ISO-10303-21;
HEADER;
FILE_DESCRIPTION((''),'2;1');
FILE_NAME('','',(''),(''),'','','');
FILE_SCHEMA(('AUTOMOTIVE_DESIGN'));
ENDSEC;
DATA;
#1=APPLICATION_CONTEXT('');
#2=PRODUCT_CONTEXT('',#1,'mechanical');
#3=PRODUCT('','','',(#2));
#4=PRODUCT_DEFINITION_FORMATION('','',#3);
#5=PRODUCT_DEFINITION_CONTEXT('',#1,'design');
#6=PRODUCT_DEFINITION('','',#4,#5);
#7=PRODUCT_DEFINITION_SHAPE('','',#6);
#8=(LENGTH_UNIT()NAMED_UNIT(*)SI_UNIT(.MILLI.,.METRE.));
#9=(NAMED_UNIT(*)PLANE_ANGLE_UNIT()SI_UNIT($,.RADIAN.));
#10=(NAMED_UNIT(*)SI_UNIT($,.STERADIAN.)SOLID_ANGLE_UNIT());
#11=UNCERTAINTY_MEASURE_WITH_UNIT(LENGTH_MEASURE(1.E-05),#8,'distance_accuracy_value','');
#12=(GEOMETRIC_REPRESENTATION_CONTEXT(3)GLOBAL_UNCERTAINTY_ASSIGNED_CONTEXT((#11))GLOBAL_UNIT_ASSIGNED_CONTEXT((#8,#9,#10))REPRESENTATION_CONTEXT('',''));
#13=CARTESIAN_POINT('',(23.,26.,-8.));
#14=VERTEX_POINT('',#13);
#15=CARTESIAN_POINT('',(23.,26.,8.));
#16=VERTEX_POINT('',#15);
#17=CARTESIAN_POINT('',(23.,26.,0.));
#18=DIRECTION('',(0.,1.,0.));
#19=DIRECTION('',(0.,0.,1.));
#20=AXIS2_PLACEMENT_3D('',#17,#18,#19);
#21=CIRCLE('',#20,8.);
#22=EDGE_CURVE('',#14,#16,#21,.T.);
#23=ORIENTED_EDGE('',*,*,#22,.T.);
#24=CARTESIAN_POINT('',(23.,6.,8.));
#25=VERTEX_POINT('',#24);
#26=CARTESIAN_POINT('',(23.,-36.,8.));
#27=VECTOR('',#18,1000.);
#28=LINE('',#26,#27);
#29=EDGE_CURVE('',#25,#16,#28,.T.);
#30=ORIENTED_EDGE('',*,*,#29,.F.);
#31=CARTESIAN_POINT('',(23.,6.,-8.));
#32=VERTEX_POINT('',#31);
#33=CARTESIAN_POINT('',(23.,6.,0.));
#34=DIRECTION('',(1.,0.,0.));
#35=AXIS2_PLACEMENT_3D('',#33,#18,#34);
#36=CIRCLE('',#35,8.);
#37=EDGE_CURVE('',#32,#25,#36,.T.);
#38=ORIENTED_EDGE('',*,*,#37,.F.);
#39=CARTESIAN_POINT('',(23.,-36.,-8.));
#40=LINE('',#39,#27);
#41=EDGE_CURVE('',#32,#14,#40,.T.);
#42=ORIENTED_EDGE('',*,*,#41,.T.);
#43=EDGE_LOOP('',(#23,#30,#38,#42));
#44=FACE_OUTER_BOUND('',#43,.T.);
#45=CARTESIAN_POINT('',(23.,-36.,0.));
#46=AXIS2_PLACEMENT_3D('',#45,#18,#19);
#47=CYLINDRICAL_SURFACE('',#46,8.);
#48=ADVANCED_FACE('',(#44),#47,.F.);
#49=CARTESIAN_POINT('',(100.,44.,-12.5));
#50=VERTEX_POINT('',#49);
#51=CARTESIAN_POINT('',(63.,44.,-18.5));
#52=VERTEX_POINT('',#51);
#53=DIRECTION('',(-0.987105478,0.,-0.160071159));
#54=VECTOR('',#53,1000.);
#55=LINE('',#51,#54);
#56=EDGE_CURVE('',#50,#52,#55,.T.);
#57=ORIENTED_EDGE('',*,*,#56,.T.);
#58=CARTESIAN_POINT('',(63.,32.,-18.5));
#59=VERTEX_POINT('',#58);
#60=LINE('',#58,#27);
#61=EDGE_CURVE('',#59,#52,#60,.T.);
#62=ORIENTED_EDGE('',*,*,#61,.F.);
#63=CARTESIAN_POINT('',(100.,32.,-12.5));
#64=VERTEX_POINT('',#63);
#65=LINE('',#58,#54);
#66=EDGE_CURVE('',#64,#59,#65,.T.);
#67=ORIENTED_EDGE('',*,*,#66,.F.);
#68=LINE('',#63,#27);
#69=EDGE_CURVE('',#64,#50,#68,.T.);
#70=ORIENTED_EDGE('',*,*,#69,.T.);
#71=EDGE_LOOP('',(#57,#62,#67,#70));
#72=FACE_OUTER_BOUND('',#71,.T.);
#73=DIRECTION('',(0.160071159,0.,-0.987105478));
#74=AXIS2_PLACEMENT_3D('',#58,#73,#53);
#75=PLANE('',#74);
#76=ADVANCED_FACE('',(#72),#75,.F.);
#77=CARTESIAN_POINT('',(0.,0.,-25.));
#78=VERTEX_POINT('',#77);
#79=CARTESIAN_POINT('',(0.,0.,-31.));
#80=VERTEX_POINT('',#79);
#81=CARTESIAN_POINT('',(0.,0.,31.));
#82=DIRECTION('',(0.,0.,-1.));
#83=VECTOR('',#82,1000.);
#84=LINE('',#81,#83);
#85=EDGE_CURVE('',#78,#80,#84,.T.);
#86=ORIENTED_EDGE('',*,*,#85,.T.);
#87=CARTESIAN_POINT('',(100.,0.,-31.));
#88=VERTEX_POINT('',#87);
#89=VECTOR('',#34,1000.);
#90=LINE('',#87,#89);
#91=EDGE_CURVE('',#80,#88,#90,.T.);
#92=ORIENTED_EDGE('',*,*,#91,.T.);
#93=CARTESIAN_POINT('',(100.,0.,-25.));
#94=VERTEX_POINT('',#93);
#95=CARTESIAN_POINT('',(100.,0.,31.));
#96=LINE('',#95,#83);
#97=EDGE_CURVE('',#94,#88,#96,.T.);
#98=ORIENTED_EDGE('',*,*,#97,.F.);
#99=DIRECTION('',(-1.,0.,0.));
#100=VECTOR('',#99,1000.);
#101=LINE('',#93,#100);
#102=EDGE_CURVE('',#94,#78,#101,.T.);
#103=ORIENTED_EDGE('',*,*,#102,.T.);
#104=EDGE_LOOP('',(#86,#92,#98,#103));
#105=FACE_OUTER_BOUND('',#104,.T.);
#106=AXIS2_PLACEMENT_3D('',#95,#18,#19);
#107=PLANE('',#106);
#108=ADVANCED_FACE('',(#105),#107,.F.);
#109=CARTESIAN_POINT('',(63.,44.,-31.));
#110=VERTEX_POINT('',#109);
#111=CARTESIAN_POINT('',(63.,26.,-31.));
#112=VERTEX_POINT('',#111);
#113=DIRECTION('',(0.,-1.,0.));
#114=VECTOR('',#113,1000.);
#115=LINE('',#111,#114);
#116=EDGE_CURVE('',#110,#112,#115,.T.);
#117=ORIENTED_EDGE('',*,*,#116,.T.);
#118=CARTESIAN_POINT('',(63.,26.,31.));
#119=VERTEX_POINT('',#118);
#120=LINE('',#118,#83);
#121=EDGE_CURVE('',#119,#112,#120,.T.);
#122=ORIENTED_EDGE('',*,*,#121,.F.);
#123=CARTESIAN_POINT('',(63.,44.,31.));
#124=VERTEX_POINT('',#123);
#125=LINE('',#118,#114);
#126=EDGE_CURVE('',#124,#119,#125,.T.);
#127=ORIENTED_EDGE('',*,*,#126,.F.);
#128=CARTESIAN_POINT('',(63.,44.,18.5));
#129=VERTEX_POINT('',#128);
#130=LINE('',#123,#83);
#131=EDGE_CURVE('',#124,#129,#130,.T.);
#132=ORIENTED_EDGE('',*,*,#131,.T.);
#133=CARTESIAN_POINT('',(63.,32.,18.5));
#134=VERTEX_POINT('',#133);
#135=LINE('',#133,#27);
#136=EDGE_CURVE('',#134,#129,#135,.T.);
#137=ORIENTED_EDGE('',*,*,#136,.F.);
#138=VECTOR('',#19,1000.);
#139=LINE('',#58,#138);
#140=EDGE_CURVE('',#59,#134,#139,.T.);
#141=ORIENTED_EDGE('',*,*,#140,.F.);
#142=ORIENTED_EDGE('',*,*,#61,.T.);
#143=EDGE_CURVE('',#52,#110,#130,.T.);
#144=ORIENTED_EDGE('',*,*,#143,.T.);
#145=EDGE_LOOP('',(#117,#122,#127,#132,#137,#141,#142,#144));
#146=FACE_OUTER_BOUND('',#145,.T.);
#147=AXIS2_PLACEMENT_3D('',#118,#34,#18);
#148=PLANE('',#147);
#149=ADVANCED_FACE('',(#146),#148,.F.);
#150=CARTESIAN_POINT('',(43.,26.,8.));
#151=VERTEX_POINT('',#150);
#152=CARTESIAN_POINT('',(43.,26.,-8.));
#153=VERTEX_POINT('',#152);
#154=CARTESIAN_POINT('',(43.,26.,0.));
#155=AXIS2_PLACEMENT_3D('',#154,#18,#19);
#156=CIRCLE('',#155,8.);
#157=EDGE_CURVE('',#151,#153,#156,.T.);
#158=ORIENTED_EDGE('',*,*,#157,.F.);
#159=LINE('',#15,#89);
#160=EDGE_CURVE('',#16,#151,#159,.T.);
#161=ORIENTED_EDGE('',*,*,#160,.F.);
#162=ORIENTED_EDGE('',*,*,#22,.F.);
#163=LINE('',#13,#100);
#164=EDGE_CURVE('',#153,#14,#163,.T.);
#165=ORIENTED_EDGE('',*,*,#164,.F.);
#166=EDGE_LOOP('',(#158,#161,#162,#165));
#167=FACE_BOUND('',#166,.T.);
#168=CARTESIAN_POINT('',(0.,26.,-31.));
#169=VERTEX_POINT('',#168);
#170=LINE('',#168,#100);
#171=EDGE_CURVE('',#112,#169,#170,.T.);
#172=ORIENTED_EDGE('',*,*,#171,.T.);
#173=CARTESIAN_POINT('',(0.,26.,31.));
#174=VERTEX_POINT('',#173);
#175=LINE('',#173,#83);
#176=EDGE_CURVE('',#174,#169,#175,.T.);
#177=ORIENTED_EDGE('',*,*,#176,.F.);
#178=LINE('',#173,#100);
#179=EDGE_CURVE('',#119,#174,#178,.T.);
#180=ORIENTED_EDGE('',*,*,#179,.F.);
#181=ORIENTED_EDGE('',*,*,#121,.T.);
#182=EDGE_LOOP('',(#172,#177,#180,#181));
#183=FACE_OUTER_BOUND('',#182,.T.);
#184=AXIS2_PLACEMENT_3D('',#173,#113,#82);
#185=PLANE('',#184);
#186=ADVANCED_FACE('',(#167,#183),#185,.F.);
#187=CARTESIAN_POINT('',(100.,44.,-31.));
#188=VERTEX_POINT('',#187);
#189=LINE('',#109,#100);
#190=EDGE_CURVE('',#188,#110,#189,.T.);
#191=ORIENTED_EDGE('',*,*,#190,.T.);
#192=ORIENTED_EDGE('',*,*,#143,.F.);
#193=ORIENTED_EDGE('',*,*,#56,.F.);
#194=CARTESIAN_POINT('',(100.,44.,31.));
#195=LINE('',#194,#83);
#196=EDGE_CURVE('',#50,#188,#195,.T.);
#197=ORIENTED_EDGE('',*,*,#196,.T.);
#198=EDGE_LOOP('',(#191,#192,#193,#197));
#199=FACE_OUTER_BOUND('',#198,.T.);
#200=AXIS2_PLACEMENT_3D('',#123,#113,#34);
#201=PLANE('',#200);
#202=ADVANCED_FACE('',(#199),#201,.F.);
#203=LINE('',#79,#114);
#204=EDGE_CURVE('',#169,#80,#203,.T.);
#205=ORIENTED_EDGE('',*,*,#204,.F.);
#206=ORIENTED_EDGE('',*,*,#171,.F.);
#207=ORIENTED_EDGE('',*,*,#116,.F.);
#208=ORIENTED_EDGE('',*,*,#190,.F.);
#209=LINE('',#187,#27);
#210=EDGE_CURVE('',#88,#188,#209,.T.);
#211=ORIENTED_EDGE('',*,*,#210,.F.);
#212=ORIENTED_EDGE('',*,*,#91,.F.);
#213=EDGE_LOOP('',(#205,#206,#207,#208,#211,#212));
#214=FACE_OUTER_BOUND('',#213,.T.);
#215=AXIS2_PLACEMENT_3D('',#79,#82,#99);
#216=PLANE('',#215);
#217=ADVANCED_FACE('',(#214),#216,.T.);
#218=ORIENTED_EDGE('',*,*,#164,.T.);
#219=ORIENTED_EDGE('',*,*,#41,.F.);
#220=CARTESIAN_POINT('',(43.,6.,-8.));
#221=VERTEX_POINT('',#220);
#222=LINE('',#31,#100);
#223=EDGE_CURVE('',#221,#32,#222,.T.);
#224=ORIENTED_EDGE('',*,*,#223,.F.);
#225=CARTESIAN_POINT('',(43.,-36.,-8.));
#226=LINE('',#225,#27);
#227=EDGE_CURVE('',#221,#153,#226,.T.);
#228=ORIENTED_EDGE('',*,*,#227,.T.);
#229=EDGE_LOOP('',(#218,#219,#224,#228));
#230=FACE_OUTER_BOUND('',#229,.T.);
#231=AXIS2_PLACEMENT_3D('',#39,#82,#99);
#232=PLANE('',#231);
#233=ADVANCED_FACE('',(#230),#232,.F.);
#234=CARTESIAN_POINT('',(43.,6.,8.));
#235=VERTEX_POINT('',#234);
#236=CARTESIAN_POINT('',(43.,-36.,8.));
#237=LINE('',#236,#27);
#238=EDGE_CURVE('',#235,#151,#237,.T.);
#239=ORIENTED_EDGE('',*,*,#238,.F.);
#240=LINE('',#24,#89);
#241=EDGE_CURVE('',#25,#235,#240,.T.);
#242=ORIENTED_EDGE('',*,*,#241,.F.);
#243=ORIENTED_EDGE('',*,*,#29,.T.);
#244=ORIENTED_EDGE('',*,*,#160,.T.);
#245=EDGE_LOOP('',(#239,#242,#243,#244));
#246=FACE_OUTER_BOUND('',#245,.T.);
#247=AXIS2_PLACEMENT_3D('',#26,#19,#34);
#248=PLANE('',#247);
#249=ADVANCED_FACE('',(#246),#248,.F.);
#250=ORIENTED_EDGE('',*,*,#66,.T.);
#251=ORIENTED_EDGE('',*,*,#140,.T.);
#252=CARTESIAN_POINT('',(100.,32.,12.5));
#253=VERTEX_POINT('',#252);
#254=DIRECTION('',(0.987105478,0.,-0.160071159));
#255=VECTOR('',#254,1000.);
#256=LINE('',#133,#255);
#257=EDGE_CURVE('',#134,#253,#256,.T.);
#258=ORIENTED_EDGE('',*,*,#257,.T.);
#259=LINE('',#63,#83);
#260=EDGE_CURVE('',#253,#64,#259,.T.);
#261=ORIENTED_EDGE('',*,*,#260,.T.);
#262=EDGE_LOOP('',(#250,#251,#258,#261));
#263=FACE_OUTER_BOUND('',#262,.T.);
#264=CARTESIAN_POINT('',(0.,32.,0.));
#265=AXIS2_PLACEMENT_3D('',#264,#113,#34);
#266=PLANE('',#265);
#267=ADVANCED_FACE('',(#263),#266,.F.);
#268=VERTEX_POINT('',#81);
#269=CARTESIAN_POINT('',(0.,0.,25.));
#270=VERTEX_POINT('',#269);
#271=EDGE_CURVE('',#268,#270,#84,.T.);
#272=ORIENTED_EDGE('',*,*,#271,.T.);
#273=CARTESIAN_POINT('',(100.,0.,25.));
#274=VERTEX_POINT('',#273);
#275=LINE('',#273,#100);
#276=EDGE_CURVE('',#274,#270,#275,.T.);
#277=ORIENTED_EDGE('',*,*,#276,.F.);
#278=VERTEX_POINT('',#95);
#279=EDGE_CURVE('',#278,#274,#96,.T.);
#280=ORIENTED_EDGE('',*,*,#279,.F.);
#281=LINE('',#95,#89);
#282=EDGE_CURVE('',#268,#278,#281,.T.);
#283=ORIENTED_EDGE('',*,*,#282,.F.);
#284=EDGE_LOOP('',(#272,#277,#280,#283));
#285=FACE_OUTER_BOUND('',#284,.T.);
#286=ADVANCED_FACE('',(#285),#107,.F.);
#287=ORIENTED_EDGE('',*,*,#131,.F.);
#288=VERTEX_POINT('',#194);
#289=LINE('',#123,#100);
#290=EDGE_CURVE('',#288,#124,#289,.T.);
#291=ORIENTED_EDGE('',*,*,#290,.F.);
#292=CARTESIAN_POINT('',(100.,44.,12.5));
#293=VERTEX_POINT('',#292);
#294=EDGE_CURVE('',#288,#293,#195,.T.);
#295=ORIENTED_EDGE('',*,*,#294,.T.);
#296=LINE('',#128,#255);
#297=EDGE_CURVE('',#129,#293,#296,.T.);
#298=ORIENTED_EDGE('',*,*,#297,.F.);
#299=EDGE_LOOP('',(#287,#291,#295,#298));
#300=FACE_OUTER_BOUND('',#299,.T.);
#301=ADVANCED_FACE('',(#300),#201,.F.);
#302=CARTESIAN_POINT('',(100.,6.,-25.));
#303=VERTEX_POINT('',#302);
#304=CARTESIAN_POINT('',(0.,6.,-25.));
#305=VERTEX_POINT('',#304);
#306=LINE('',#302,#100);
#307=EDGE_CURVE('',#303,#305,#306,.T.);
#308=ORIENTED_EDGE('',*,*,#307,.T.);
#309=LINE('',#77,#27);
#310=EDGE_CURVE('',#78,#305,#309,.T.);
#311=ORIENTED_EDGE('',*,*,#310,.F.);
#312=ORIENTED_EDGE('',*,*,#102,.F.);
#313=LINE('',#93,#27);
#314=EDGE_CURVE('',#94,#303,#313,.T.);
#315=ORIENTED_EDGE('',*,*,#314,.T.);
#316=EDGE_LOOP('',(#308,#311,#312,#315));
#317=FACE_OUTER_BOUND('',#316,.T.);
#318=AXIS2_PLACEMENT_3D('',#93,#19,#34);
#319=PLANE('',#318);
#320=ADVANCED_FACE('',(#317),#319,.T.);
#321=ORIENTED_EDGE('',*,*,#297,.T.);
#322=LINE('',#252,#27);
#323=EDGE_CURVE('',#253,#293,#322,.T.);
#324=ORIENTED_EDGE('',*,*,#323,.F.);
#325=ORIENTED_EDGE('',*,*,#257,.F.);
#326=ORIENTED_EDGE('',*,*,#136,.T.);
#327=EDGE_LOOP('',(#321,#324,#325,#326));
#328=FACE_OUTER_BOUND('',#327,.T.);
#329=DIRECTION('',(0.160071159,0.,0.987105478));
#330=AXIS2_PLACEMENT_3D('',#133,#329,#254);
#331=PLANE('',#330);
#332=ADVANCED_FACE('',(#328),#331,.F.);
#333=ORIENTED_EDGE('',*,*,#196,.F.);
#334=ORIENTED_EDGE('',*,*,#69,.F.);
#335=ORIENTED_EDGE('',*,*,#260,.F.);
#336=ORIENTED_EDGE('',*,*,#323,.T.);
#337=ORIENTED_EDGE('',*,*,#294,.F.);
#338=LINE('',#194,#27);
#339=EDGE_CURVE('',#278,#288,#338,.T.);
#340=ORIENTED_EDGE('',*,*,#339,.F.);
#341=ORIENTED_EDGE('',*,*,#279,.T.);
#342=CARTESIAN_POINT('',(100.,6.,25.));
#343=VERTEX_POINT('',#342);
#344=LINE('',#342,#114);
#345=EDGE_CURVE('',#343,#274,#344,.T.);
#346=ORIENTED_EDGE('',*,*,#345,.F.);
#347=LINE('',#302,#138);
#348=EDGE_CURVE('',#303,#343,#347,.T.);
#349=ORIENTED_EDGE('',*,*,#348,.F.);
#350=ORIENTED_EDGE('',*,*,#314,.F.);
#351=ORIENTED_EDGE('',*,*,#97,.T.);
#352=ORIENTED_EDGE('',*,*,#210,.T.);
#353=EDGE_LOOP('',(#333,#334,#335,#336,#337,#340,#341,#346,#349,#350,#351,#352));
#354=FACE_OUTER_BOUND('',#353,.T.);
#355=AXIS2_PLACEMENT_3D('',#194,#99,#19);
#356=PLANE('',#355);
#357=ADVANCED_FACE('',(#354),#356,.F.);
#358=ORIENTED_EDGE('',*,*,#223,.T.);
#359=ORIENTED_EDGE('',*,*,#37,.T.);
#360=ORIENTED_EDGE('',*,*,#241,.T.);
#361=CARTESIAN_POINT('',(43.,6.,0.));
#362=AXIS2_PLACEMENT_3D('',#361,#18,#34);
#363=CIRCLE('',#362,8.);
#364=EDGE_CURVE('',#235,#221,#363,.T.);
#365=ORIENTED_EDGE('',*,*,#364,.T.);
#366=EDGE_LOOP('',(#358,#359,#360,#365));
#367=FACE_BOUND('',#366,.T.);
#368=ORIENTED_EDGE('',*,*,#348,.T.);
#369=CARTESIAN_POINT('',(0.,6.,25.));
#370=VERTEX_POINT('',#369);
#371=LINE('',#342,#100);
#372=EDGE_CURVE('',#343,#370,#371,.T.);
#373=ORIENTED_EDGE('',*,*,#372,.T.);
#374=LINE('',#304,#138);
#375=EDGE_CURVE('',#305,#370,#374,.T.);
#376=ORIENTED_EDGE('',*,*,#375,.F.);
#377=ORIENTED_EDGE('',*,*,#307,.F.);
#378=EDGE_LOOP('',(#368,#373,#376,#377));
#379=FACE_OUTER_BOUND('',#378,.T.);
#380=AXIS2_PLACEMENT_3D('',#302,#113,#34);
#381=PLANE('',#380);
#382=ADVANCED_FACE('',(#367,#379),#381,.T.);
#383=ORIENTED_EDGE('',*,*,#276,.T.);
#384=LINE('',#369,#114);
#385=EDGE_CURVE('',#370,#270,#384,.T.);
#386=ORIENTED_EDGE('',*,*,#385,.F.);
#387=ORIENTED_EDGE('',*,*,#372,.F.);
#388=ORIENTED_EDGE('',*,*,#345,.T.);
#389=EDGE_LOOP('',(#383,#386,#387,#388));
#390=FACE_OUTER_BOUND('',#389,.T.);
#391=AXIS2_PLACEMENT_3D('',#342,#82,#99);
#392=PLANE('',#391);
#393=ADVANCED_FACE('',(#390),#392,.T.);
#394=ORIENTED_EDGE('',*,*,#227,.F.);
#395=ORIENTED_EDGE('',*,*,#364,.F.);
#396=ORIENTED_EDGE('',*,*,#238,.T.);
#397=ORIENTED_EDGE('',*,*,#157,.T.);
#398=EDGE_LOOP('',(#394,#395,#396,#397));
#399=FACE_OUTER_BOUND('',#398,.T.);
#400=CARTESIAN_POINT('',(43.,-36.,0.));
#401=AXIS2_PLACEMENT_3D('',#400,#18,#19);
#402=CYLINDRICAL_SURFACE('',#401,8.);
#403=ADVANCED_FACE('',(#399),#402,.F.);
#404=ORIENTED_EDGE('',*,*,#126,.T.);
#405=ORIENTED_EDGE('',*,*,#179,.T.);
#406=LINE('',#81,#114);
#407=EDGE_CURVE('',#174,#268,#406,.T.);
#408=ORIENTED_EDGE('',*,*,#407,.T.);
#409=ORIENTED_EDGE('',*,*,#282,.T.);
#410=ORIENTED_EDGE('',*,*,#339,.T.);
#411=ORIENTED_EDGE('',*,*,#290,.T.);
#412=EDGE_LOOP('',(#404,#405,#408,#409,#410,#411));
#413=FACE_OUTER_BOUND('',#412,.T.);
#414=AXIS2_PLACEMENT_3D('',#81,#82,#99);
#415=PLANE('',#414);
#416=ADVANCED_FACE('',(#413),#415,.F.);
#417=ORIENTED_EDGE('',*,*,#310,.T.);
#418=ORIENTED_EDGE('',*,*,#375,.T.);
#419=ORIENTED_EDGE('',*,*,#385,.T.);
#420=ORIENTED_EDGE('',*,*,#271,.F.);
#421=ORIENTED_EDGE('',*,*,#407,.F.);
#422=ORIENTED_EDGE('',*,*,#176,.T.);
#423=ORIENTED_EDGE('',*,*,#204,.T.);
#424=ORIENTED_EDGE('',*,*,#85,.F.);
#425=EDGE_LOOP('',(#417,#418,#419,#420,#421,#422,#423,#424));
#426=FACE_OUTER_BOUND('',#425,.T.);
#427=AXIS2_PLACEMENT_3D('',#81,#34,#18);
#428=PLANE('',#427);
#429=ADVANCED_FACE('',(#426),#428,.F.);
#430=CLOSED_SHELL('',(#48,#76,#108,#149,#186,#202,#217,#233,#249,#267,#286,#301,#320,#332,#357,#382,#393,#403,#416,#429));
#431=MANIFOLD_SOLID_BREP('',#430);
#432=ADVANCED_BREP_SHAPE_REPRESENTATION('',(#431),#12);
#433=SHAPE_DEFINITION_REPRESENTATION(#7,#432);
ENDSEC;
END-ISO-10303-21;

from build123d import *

# Parameters (mm, degrees)
BASE_BLOCK_DEPTH              = 31
STEPPED_CHANNEL_THROUGH_DEPTH = 62
TOP_SLOT_POCKET_12_DEEP_DEPTH = 12
BOTTOM_GROOVE_SKETCH_W        = 50
BOTTOM_GROOVE_SKETCH_H        = 6
BOTTOM_GROOVE_6X6_DEPTH       = 114.564959384


with BuildPart() as part:
    # Base Profile Sketch → Base Block (new, symmetric)
    with BuildSketch(Plane.XY):
        Polygon((0, 0), (0, 26), (63, 26), (63, 44), (100, 44), (100, 0), align=None)
    extrude(amount=BASE_BLOCK_DEPTH, both=True)

    # Stepped Channel Sketch → Stepped Channel Through (cut)
    with BuildSketch(Plane(origin=(0, 26, 0), x_dir=(1, 0, 0), z_dir=(0, 1, 0))):
        with BuildLine():
            Line((23, 8), (43, 8))
            ThreePointArc((43, 8), (51, 0), (43, -8))
            Line((43, -8), (23, -8))
            ThreePointArc((23, -8), (15, 0), (23, 8))
        make_face()
    extrude(amount=-STEPPED_CHANNEL_THROUGH_DEPTH, mode=Mode.SUBTRACT)

    # Top Slot Sketch → Top Slot Pocket 12 Deep (cut)
    with BuildSketch(Plane(origin=(0, 44, 0), x_dir=(1, 0, 0), z_dir=(0, 1, 0))):
        Polygon((63, 18.5), (63, -18.5), (100, -12.5), (100, 12.5), align=None)
    extrude(amount=-TOP_SLOT_POCKET_12_DEEP_DEPTH, mode=Mode.SUBTRACT)

    # Bottom Groove Sketch → Bottom Groove 6x6 (cut, through all)
    with BuildSketch(Plane.ZY):
        with Locations((0, 3)):
            Rectangle(BOTTOM_GROOVE_SKETCH_W, BOTTOM_GROOVE_SKETCH_H)
    extrude(amount=-BOTTOM_GROOVE_6X6_DEPTH, mode=Mode.SUBTRACT)


solid = part.part
